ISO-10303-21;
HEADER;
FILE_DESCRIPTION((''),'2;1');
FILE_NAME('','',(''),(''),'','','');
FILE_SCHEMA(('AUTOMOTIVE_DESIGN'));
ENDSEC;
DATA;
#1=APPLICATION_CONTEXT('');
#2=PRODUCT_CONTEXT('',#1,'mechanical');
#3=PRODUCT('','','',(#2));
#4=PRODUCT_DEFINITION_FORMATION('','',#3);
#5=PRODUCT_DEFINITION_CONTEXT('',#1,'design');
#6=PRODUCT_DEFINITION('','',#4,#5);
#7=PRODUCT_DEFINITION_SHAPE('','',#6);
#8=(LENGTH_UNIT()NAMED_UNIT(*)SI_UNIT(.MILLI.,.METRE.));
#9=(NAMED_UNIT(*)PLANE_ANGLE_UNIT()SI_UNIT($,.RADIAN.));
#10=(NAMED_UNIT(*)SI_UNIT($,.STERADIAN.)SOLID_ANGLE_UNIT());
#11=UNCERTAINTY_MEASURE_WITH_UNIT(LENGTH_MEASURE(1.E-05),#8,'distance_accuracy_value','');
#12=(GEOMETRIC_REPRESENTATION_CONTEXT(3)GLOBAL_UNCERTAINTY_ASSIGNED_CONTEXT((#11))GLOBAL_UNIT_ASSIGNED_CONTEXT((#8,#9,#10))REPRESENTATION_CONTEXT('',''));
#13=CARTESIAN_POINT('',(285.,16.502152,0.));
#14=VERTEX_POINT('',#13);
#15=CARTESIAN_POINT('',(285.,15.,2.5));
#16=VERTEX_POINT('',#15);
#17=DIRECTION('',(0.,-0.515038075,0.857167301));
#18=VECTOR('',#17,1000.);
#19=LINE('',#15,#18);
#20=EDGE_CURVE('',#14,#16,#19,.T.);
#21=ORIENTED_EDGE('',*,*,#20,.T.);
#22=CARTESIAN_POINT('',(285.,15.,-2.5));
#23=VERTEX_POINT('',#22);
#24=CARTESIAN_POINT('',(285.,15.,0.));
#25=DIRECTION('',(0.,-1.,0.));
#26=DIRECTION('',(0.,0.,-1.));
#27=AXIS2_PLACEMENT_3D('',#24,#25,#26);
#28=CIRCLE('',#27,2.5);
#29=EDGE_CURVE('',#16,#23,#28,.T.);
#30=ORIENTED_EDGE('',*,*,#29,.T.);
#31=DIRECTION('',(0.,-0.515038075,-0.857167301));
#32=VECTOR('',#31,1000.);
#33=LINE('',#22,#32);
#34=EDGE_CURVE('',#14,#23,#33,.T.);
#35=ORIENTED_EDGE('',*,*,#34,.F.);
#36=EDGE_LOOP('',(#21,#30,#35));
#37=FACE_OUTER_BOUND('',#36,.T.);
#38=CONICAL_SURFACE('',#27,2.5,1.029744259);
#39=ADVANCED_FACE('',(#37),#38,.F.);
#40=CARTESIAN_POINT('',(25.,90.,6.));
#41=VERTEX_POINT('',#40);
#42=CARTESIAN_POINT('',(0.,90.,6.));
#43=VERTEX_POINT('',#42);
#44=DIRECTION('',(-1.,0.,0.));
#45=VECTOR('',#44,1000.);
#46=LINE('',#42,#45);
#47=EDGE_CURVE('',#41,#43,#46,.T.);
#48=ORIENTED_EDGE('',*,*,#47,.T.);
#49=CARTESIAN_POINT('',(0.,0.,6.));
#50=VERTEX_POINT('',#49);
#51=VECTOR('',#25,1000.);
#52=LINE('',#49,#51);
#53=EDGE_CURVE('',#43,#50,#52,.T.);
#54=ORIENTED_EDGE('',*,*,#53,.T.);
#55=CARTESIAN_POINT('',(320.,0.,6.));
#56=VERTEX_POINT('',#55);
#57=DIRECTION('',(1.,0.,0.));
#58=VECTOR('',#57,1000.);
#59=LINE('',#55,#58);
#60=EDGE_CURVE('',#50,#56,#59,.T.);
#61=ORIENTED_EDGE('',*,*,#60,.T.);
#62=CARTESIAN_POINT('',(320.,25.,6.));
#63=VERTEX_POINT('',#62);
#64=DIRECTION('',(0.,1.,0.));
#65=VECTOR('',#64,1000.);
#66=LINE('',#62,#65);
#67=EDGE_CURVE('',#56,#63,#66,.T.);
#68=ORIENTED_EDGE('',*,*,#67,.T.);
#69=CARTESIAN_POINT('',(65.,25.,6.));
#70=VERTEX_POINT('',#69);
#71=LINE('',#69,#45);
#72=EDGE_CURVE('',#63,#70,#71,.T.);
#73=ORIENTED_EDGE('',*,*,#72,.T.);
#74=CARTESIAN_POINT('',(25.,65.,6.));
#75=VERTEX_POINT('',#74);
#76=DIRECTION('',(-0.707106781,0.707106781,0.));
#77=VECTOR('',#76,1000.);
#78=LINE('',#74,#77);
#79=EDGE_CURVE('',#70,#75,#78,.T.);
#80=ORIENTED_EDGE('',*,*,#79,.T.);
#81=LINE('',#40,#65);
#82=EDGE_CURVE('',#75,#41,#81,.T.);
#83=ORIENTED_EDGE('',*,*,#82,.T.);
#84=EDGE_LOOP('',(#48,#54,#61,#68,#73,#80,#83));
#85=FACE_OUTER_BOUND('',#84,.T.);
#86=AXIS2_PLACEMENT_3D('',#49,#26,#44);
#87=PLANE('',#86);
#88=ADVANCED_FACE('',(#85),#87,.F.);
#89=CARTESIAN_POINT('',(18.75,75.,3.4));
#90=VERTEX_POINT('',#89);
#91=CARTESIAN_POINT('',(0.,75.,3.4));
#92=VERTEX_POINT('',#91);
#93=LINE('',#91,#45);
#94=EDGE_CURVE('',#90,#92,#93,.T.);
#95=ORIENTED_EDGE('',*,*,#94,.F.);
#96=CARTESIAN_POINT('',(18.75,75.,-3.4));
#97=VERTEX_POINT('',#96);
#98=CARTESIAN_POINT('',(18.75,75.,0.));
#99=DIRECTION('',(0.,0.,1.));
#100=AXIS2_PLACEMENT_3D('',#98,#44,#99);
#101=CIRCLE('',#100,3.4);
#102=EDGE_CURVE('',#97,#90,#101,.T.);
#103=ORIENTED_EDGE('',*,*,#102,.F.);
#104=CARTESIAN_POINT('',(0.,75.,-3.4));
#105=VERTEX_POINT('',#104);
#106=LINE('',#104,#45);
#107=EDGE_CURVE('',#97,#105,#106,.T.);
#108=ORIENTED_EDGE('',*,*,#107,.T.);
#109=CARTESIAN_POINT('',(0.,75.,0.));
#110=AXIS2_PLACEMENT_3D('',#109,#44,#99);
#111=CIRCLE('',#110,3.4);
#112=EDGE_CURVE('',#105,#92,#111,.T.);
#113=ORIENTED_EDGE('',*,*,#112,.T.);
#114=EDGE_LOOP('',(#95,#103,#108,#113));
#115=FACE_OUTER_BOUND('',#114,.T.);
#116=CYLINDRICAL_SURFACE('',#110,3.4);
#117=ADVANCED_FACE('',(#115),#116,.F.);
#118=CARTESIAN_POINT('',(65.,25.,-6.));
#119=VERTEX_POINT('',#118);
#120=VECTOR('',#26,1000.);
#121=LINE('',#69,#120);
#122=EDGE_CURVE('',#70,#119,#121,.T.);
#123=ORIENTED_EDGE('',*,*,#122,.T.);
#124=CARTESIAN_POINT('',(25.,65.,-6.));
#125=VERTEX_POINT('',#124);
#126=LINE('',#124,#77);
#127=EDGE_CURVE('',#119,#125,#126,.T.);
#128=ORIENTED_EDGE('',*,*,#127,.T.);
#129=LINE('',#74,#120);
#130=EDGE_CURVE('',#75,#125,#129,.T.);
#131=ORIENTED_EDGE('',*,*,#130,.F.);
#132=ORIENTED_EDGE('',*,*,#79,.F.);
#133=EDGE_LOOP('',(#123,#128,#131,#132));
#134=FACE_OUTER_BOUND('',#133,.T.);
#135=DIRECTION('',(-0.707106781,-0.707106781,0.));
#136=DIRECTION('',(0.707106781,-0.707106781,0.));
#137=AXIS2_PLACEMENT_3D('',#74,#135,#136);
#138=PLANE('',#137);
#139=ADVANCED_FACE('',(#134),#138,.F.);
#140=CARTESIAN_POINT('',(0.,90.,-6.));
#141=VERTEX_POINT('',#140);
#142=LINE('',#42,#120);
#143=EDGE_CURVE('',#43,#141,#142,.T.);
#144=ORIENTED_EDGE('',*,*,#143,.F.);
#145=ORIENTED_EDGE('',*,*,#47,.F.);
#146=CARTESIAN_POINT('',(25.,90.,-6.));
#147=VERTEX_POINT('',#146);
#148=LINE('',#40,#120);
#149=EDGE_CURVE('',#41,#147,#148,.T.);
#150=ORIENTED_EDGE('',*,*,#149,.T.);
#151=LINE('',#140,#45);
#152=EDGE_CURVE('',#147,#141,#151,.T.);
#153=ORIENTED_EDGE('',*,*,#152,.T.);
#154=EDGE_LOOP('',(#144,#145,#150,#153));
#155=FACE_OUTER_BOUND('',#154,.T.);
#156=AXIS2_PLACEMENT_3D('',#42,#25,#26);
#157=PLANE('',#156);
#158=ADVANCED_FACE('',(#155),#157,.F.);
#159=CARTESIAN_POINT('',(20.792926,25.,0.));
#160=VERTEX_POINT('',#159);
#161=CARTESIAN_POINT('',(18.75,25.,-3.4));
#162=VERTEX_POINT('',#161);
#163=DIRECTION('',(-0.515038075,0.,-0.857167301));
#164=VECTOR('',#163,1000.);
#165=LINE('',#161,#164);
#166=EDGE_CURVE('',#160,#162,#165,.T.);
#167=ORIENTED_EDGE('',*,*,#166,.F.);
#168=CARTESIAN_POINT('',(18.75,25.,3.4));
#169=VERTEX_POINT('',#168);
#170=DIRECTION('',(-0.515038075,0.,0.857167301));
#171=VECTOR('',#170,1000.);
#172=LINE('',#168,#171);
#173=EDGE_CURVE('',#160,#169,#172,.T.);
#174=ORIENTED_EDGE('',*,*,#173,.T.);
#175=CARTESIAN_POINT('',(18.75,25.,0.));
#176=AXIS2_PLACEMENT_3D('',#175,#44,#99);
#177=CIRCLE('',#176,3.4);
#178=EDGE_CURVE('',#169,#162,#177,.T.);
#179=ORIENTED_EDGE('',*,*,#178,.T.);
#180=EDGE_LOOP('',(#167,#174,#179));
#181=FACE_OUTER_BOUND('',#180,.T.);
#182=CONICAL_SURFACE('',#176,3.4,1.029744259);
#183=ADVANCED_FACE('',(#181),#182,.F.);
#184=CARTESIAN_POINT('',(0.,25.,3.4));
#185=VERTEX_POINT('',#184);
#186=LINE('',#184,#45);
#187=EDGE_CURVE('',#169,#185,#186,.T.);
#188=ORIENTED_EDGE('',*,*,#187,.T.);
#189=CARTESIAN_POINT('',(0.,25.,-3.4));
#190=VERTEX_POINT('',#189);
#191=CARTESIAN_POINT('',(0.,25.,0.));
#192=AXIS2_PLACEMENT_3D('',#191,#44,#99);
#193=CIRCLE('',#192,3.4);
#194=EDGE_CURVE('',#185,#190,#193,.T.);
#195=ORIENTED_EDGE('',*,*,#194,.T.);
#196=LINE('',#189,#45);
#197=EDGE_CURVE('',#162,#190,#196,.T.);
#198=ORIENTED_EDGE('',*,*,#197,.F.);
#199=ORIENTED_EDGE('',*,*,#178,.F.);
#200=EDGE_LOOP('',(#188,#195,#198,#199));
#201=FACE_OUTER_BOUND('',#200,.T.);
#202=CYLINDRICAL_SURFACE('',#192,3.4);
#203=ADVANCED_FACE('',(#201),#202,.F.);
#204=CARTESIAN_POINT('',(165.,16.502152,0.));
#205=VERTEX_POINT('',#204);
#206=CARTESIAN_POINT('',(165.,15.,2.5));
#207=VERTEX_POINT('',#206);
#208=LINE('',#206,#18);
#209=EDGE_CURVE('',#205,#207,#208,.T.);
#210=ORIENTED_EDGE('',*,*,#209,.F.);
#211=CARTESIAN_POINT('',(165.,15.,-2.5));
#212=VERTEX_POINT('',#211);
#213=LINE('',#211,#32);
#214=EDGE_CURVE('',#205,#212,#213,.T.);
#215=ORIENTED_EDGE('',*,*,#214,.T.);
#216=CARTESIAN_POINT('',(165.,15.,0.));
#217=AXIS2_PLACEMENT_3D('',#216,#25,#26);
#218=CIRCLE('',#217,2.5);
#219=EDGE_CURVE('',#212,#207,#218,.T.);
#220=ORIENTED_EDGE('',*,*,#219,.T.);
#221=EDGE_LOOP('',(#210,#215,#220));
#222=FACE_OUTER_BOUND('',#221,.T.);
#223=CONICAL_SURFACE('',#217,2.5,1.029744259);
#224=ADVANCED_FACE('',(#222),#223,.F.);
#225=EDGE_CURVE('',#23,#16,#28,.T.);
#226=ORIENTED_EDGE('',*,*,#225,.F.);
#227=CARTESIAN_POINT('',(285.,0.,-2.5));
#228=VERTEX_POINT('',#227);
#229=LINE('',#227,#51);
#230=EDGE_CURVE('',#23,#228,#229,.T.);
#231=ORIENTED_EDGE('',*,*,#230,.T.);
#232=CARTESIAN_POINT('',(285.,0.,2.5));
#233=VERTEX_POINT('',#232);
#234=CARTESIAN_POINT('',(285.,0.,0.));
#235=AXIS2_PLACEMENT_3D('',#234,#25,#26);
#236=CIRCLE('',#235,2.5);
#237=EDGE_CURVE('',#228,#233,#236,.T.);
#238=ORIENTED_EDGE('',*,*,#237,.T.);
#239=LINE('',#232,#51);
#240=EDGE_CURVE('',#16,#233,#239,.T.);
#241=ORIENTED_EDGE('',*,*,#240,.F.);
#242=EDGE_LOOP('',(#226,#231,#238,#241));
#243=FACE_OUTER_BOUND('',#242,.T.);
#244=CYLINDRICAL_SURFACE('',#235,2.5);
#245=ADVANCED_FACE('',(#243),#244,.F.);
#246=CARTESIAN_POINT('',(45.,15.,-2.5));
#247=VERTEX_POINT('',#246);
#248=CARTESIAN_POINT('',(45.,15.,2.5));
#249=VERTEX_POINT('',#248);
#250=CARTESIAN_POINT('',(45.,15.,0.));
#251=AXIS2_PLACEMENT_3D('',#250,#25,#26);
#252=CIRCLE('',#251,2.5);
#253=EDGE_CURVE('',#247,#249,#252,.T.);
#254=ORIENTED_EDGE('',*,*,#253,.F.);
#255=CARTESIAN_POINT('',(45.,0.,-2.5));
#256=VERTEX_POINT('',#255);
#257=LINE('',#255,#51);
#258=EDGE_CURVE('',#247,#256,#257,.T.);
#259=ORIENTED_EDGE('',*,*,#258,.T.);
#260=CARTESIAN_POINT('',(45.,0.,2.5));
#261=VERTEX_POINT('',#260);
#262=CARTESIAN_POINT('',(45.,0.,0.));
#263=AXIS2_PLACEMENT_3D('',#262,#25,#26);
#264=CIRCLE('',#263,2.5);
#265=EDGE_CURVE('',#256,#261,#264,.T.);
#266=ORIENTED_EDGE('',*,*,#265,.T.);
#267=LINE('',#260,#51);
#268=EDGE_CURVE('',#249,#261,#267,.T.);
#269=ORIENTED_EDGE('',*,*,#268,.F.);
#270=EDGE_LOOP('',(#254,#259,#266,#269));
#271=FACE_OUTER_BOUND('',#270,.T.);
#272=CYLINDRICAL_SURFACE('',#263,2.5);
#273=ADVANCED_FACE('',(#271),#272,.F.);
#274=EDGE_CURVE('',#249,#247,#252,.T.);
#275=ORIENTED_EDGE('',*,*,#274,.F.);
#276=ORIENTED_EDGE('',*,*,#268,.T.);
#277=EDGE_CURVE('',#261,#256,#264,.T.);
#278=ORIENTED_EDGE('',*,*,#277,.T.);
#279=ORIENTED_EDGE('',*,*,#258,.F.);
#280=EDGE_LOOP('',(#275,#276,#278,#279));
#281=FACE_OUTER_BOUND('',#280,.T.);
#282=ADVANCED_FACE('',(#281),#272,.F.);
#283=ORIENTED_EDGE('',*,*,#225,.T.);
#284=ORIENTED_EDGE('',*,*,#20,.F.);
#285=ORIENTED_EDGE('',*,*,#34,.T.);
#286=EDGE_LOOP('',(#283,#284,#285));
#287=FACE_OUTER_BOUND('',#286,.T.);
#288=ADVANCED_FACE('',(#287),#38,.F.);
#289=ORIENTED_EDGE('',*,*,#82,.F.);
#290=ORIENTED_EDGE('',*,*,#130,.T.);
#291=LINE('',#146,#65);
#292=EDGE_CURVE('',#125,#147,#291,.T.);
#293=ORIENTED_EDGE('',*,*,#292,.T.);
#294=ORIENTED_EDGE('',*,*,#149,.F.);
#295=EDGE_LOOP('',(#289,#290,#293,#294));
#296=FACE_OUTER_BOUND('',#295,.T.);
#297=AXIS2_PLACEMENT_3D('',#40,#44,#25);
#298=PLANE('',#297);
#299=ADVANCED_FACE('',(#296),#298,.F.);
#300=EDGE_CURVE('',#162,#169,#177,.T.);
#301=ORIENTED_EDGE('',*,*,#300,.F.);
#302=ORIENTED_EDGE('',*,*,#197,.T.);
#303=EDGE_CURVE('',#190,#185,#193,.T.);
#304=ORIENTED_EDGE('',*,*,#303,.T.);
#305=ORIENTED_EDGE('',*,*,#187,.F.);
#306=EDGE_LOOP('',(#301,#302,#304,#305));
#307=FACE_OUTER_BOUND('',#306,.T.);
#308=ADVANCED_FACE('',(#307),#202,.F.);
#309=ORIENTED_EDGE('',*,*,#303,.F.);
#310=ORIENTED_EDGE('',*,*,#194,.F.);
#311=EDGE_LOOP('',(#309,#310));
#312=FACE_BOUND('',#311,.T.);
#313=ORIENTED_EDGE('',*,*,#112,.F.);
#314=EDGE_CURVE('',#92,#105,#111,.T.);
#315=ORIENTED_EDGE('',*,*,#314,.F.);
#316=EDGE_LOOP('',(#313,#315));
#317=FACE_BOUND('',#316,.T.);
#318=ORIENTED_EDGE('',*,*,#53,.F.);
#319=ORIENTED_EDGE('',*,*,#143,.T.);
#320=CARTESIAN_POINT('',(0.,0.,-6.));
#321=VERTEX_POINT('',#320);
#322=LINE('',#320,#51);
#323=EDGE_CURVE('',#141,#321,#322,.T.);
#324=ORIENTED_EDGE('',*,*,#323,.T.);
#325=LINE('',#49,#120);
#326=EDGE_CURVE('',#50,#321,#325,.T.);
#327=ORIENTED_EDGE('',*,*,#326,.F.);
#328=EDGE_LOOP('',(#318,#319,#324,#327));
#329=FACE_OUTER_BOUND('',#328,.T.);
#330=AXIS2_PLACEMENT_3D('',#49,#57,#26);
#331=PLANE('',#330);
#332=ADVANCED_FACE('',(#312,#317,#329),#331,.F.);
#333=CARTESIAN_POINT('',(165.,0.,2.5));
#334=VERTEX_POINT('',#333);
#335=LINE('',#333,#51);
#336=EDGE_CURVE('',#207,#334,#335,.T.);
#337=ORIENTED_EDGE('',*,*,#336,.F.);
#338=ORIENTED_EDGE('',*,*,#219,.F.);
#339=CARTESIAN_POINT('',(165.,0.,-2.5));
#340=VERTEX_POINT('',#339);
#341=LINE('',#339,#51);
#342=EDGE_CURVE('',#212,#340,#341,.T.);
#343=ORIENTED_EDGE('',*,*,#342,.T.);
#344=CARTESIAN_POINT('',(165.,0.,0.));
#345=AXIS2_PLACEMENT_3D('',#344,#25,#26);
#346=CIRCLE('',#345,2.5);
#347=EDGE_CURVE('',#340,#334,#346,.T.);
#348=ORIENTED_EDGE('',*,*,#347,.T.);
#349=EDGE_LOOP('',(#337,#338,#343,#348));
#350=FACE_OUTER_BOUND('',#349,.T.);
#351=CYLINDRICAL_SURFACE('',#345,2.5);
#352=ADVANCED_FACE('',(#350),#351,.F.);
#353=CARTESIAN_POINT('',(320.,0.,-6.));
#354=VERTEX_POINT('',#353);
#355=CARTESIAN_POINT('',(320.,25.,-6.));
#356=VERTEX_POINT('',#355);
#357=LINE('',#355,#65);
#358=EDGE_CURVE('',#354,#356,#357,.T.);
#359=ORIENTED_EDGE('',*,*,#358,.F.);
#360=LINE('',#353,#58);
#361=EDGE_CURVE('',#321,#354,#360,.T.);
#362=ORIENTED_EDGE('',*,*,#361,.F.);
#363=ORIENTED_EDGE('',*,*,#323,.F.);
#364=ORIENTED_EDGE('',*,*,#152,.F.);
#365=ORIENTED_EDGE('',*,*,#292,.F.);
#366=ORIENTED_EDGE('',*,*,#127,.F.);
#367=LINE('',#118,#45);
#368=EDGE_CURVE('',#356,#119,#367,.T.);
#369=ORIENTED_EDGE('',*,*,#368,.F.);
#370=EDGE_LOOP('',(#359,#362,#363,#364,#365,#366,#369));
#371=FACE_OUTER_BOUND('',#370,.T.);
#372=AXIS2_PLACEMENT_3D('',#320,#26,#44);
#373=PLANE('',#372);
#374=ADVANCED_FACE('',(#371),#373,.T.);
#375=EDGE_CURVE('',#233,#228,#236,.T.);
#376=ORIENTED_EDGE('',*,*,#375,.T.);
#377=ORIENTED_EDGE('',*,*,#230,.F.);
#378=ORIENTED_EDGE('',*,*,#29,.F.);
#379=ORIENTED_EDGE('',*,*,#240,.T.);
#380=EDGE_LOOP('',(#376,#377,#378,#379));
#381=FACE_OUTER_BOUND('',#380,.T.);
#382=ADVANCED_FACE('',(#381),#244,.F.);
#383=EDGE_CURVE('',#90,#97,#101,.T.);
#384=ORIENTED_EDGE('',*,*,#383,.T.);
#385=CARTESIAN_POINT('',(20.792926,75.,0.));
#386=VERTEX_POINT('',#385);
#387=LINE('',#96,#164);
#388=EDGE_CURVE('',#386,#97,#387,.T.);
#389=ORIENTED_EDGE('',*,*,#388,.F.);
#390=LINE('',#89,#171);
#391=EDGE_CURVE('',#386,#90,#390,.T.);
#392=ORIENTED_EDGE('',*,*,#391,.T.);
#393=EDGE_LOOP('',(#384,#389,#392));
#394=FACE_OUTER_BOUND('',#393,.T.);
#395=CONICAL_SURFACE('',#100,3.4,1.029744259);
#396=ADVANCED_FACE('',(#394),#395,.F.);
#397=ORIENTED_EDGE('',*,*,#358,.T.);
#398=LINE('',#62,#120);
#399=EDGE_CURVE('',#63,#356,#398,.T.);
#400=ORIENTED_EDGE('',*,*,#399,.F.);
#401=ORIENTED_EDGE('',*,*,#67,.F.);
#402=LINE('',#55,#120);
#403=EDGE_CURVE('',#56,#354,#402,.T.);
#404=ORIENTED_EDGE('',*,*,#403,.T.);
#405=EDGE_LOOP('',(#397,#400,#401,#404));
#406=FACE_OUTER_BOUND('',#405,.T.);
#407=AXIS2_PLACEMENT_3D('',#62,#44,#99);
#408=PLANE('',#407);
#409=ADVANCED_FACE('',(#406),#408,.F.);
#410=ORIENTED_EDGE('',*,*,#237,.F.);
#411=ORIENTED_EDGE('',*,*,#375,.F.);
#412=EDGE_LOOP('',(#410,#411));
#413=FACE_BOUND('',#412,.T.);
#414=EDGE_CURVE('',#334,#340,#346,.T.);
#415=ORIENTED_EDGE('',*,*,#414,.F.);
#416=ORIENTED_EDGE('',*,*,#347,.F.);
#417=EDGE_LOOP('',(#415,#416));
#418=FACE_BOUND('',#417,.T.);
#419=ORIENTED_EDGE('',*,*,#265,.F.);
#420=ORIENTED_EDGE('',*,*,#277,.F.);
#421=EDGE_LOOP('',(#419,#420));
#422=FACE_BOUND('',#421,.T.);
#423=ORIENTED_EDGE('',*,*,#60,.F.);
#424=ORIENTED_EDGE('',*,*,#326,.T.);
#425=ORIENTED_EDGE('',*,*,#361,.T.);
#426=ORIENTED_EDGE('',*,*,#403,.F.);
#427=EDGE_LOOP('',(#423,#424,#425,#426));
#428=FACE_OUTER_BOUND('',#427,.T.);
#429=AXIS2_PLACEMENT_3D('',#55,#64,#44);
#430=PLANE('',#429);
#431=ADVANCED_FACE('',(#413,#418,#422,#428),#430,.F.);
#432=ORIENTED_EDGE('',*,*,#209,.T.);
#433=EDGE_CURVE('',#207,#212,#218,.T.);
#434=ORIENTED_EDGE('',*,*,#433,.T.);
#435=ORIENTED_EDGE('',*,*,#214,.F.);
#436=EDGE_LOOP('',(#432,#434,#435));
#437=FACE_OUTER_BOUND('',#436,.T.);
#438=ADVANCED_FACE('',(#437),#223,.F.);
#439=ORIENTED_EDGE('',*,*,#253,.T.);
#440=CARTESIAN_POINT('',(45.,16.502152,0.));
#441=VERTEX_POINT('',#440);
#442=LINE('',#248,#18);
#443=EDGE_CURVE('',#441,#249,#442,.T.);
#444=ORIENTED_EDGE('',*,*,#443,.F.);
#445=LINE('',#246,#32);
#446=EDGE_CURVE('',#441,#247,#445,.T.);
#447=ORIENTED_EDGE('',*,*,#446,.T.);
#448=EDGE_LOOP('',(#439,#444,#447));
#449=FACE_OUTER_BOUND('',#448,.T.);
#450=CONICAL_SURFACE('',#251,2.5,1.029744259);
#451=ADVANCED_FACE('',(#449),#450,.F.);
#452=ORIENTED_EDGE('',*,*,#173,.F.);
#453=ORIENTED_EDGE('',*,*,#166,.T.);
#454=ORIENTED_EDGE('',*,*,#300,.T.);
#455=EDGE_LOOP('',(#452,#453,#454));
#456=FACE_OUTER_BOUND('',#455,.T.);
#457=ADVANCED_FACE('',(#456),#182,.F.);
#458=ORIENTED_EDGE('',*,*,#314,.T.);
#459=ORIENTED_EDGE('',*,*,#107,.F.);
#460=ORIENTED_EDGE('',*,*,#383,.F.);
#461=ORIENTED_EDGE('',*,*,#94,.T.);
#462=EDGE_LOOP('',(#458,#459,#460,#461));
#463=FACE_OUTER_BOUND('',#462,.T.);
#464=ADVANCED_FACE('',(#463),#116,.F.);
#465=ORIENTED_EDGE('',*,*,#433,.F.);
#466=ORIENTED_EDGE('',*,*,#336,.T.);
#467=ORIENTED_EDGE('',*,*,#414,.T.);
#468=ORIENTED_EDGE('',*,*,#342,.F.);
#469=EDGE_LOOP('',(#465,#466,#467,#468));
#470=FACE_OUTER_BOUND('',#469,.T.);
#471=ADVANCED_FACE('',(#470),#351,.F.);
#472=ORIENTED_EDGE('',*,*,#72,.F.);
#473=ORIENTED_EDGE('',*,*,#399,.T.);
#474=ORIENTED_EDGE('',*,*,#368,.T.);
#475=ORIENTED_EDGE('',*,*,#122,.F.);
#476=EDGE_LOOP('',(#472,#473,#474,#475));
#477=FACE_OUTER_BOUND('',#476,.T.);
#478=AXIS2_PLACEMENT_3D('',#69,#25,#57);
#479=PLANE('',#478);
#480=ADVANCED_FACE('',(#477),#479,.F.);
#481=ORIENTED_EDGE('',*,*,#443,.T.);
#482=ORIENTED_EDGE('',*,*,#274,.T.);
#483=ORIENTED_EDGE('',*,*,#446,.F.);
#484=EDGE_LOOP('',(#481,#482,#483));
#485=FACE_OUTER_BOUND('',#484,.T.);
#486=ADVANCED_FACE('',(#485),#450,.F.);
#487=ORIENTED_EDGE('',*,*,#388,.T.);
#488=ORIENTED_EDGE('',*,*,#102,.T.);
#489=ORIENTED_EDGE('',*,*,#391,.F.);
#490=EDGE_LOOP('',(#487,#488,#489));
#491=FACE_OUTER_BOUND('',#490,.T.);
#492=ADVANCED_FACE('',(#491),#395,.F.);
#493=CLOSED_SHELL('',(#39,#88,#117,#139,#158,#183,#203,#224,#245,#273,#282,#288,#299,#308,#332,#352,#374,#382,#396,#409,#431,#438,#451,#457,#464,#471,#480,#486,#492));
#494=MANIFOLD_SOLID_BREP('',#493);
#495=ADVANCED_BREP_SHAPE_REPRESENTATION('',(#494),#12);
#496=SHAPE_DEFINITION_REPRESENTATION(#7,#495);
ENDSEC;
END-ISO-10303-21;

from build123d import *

# Parameters (mm, degrees)
EXTRUDE_1_DEPTH        = 6
HOLE_WIZARD_M8_1_D     = 6.8
HOLE_WIZARD_M8_1_DEPTH = 18.75
HOLE_WIZARD_M8_1_TIP   = 2.042926105
HOLE_WIZARD_M6_1_D     = 5
HOLE_WIZARD_M6_1_DEPTH = 15
HOLE_WIZARD_M6_1_TIP   = 1.502151548


with BuildPart() as part:
    # 草图1 → 凸台-拉伸1 (new, symmetric)
    with BuildSketch(Plane.XY):
        Polygon((0, 0), (0, 90), (25, 90), (25, 65), (65, 25), (320, 25), (320, 0), align=None)
    extrude(amount=EXTRUDE_1_DEPTH, both=True)

    # M8 螺纹孔1
    with Locations(Plane(origin=(0, 75, 0), x_dir=(0, 0, -1), z_dir=(-1, 0, 0))):
        with Locations((0, 0), (0, 50)):
            Hole(HOLE_WIZARD_M8_1_D / 2, depth=HOLE_WIZARD_M8_1_DEPTH)
            with Locations((0, 0, -(HOLE_WIZARD_M8_1_DEPTH + HOLE_WIZARD_M8_1_TIP / 2))):  # 118° drill point
                Cone(0, HOLE_WIZARD_M8_1_D / 2, HOLE_WIZARD_M8_1_TIP, mode=Mode.SUBTRACT)

    # M6 螺纹孔1
    with Locations(Plane(origin=(45, 0, 0), x_dir=(0, 0, -1), z_dir=(0, -1, 0))):
        with Locations((0, 0), (0, 120), (0, 240)):
            Hole(HOLE_WIZARD_M6_1_D / 2, depth=HOLE_WIZARD_M6_1_DEPTH)
            with Locations((0, 0, -(HOLE_WIZARD_M6_1_DEPTH + HOLE_WIZARD_M6_1_TIP / 2))):  # 118° drill point
                Cone(0, HOLE_WIZARD_M6_1_D / 2, HOLE_WIZARD_M6_1_TIP, mode=Mode.SUBTRACT)


solid = part.part
